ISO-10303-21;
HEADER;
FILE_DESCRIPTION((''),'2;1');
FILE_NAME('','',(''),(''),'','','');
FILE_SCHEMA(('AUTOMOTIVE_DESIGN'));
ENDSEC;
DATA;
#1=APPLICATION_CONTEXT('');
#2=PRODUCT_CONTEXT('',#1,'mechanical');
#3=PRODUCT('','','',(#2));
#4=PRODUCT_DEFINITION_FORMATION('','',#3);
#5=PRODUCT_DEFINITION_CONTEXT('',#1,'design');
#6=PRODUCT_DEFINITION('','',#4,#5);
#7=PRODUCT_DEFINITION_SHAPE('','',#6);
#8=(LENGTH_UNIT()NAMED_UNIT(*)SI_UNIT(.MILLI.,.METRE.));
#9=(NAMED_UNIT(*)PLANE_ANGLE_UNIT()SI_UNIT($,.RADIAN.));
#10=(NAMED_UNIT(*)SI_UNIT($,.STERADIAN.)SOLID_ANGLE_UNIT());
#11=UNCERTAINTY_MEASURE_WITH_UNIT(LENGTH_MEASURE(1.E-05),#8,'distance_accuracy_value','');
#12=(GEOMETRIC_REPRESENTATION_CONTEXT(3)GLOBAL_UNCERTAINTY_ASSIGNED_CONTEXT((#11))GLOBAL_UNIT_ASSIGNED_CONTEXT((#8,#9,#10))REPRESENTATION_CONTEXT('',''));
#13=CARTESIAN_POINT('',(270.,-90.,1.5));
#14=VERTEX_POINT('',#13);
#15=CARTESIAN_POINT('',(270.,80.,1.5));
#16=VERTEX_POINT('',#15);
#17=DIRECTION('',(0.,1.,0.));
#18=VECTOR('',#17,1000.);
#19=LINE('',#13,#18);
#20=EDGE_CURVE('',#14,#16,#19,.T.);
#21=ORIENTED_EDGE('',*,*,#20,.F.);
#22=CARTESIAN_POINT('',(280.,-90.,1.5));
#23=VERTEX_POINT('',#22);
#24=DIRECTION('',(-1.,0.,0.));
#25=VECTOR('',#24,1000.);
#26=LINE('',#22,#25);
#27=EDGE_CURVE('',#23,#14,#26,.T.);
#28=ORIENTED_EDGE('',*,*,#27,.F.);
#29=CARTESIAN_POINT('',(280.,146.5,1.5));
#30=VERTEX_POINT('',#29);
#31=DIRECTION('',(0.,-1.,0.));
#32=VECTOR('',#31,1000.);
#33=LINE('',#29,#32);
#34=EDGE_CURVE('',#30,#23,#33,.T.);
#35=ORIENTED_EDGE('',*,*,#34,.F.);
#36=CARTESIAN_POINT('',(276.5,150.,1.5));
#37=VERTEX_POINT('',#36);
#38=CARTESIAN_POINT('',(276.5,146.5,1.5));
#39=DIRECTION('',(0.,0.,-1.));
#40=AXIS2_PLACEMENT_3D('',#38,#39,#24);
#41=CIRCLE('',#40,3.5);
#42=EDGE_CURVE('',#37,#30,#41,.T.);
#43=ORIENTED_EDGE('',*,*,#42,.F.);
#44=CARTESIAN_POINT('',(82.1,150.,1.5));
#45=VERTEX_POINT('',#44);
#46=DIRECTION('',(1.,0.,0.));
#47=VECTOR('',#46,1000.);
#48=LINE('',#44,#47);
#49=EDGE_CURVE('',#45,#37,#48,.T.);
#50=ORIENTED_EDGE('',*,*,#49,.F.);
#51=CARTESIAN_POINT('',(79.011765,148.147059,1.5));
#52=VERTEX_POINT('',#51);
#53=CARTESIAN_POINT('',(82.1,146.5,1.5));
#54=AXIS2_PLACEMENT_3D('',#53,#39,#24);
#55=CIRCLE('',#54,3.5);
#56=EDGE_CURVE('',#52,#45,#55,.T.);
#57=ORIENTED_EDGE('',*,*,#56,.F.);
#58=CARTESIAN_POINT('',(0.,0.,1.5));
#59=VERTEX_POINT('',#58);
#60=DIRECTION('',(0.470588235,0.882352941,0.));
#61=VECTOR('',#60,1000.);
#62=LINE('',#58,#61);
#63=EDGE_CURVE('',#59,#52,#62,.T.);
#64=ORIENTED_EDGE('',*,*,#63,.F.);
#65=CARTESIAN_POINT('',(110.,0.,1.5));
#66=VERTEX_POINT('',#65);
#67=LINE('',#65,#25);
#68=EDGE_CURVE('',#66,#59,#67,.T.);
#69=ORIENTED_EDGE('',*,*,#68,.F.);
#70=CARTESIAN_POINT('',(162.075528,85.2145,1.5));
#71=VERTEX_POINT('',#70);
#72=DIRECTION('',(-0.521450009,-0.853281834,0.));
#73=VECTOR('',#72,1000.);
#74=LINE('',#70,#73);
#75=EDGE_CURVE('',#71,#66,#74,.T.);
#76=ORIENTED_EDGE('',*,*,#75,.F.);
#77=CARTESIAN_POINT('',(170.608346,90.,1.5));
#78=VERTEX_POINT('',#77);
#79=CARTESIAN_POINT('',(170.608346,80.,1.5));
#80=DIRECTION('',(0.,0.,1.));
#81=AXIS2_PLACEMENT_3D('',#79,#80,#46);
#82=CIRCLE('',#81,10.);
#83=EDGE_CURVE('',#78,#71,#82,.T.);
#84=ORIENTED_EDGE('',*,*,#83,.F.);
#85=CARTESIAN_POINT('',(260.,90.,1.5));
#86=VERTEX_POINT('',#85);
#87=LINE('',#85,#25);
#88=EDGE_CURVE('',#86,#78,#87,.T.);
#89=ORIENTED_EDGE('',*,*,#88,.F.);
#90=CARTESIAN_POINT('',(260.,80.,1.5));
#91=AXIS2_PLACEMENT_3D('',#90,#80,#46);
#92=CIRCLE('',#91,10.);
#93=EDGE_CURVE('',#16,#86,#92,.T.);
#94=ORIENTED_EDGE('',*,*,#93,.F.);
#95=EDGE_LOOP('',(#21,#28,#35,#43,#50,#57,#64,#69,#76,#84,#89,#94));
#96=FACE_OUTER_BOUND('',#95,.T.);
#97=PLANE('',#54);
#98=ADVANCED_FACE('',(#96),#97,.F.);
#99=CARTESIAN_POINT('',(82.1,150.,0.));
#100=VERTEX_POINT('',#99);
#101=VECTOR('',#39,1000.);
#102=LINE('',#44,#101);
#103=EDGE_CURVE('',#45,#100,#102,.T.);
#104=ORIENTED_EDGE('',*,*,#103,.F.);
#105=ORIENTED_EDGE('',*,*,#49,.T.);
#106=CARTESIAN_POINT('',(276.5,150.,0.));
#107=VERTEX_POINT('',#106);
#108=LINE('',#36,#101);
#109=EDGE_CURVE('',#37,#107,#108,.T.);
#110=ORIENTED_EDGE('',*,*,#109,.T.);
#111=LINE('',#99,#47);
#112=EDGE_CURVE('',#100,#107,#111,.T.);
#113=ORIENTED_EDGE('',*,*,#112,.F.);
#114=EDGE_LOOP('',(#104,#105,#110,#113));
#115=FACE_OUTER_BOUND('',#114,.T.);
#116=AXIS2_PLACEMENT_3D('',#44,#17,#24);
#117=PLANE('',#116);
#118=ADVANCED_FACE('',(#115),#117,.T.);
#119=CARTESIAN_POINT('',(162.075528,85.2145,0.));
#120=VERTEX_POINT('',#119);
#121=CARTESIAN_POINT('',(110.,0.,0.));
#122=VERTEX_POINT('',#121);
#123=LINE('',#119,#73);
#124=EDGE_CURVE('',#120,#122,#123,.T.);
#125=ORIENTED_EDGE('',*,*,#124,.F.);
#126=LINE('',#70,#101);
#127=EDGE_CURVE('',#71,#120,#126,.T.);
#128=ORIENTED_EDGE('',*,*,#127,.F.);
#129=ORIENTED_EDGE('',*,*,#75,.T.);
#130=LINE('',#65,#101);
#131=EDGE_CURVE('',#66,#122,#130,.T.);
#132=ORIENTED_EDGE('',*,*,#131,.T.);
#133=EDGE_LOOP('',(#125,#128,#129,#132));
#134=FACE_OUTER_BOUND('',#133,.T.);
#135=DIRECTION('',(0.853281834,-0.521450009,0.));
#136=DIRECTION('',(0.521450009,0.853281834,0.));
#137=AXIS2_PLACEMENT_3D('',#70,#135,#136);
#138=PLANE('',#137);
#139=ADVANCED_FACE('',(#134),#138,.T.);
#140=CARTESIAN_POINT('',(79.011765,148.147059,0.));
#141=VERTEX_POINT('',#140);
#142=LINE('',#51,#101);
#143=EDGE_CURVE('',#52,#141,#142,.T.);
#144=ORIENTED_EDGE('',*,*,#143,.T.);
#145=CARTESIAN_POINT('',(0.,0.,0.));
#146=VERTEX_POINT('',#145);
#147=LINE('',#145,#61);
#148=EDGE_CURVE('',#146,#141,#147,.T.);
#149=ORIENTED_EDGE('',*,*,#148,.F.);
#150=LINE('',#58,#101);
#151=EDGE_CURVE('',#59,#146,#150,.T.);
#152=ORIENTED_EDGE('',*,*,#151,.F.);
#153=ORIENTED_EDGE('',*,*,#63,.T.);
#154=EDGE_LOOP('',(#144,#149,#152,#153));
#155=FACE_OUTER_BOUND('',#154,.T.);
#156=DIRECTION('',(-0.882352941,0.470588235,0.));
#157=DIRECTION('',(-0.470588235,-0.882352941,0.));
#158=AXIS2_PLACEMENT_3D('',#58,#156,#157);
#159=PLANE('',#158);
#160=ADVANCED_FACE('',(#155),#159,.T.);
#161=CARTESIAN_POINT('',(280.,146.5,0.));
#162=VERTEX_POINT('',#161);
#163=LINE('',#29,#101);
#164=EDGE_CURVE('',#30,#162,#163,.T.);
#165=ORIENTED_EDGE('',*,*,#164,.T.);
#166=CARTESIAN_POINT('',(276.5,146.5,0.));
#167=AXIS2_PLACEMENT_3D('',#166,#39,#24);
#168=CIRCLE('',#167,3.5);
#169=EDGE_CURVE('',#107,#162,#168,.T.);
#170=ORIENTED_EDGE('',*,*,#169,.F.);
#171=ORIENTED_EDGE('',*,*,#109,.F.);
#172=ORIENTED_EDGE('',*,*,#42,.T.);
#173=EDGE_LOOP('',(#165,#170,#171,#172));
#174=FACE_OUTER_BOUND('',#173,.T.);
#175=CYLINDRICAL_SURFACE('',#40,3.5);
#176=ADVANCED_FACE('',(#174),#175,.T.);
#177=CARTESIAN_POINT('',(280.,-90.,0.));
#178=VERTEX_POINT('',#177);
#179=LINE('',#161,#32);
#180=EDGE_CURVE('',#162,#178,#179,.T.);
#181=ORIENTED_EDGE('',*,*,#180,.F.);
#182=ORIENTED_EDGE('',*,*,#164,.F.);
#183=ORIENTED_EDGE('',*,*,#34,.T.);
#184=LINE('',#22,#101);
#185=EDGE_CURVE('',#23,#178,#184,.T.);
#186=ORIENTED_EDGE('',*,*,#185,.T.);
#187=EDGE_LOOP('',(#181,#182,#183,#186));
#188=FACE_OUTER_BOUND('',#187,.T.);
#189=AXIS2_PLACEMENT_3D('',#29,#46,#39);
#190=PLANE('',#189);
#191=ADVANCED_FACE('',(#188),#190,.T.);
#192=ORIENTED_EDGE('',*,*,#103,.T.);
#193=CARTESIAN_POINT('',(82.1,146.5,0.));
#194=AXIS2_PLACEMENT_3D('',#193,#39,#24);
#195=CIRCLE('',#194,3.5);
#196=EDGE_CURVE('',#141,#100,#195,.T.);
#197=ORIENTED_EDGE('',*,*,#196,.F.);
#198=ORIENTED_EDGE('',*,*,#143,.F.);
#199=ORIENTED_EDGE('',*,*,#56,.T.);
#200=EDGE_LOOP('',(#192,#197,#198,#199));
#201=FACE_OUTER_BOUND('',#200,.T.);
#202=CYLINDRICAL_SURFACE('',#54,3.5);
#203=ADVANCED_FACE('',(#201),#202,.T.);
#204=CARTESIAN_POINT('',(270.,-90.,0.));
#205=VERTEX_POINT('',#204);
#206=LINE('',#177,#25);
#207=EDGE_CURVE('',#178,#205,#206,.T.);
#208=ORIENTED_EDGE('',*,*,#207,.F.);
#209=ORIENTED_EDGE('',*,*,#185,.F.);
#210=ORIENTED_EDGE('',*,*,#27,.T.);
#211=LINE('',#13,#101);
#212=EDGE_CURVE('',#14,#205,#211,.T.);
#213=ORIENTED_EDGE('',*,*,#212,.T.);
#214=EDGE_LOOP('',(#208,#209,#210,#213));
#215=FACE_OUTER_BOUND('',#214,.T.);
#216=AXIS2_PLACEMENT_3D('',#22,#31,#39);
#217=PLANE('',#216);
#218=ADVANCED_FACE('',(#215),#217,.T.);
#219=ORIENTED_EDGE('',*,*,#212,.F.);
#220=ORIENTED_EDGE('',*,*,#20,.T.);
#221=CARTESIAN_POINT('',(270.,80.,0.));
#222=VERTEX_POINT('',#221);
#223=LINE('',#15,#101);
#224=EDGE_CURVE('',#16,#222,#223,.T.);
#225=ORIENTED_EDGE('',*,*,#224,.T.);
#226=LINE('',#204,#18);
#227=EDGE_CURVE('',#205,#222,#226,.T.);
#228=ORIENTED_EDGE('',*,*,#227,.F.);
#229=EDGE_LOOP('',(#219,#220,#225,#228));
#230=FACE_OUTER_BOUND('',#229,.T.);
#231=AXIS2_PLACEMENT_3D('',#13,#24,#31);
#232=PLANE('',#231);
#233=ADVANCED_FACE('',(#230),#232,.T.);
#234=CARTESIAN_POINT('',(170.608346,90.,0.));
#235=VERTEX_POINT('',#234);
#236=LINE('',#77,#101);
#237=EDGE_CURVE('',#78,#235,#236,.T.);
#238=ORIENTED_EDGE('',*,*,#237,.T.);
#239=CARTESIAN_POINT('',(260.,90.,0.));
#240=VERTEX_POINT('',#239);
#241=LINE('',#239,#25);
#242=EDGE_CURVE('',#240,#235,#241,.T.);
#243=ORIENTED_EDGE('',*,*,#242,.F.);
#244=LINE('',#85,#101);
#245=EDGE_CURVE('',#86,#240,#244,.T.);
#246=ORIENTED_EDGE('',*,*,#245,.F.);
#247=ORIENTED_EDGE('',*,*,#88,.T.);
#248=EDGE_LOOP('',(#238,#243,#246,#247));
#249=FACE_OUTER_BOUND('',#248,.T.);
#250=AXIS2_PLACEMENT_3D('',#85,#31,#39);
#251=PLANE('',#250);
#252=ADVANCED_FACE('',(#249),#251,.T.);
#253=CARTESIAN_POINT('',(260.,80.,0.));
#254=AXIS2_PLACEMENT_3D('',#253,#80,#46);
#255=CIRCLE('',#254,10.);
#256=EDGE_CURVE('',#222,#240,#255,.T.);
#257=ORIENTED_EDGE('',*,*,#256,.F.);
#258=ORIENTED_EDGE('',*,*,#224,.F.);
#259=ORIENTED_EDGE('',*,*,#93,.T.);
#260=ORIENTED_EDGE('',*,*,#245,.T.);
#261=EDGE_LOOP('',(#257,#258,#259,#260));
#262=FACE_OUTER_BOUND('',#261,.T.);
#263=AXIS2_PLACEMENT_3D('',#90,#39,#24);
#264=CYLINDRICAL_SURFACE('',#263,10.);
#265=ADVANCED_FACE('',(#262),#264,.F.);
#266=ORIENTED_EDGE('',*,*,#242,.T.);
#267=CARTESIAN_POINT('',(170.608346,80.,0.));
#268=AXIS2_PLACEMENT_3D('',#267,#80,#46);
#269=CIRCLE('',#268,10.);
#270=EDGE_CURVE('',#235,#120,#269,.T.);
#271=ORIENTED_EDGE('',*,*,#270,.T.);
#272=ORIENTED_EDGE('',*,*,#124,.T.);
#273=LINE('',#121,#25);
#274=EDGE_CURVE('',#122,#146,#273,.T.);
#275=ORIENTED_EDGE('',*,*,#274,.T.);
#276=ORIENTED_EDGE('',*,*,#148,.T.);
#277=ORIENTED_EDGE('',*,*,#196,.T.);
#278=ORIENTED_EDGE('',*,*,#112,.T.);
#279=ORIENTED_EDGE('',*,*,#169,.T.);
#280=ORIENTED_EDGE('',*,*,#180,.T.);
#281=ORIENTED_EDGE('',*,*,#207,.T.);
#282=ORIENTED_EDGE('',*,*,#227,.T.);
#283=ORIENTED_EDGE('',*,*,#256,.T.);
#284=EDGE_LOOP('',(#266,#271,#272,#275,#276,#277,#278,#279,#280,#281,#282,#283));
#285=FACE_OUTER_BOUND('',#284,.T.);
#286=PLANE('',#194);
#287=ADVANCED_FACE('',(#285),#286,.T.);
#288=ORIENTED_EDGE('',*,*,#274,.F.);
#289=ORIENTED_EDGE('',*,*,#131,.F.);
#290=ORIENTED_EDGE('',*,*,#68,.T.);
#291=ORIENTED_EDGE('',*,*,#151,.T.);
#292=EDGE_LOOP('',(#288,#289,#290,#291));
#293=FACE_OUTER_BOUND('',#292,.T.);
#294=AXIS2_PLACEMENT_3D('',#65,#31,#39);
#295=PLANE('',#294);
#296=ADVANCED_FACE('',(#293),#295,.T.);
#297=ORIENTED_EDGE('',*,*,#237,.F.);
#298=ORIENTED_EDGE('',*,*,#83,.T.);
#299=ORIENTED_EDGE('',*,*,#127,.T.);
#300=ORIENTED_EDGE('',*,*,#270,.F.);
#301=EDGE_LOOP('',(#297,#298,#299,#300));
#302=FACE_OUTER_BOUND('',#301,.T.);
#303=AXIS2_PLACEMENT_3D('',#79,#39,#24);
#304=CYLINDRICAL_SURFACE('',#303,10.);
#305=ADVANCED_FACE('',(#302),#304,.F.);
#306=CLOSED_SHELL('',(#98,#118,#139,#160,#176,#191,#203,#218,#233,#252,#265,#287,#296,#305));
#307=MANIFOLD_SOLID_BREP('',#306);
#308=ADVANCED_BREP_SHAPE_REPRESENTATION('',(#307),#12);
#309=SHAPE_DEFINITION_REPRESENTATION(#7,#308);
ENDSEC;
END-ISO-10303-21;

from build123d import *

# Parameters (mm, degrees)
BOSS_EXTRUDE1_DEPTH = 1.5


with BuildPart() as part:
    # Sketch1 → Boss-Extrude1 (new body)
    with BuildSketch(Plane.XY):
        with BuildLine():
            Line((0, 0), (79.011764706, 148.147058824))
            ThreePointArc((79.011764706, 148.147058824), (80.299264856, 149.50122524), (82.1, 150))
            Line((82.1, 150), (276.5, 150))
            ThreePointArc((276.5, 150), (278.974873734, 148.974873734), (280, 146.5))
            Line((280, 146.5), (280, -90))
            Line((280, -90), (270, -90))
            Line((270, -90), (270, 80))
            ThreePointArc((270, 80), (267.071067812, 87.071067812), (260, 90))
            Line((260, 90), (170.608346172, 90))
            ThreePointArc((170.608346172, 90), (165.716771832, 88.721955083), (162.075527836, 85.214500095))
            Line((162.075527836, 85.214500095), (110, 0))
            Line((110, 0), (0, 0))
        make_face()
    extrude(amount=BOSS_EXTRUDE1_DEPTH)


solid = part.part
